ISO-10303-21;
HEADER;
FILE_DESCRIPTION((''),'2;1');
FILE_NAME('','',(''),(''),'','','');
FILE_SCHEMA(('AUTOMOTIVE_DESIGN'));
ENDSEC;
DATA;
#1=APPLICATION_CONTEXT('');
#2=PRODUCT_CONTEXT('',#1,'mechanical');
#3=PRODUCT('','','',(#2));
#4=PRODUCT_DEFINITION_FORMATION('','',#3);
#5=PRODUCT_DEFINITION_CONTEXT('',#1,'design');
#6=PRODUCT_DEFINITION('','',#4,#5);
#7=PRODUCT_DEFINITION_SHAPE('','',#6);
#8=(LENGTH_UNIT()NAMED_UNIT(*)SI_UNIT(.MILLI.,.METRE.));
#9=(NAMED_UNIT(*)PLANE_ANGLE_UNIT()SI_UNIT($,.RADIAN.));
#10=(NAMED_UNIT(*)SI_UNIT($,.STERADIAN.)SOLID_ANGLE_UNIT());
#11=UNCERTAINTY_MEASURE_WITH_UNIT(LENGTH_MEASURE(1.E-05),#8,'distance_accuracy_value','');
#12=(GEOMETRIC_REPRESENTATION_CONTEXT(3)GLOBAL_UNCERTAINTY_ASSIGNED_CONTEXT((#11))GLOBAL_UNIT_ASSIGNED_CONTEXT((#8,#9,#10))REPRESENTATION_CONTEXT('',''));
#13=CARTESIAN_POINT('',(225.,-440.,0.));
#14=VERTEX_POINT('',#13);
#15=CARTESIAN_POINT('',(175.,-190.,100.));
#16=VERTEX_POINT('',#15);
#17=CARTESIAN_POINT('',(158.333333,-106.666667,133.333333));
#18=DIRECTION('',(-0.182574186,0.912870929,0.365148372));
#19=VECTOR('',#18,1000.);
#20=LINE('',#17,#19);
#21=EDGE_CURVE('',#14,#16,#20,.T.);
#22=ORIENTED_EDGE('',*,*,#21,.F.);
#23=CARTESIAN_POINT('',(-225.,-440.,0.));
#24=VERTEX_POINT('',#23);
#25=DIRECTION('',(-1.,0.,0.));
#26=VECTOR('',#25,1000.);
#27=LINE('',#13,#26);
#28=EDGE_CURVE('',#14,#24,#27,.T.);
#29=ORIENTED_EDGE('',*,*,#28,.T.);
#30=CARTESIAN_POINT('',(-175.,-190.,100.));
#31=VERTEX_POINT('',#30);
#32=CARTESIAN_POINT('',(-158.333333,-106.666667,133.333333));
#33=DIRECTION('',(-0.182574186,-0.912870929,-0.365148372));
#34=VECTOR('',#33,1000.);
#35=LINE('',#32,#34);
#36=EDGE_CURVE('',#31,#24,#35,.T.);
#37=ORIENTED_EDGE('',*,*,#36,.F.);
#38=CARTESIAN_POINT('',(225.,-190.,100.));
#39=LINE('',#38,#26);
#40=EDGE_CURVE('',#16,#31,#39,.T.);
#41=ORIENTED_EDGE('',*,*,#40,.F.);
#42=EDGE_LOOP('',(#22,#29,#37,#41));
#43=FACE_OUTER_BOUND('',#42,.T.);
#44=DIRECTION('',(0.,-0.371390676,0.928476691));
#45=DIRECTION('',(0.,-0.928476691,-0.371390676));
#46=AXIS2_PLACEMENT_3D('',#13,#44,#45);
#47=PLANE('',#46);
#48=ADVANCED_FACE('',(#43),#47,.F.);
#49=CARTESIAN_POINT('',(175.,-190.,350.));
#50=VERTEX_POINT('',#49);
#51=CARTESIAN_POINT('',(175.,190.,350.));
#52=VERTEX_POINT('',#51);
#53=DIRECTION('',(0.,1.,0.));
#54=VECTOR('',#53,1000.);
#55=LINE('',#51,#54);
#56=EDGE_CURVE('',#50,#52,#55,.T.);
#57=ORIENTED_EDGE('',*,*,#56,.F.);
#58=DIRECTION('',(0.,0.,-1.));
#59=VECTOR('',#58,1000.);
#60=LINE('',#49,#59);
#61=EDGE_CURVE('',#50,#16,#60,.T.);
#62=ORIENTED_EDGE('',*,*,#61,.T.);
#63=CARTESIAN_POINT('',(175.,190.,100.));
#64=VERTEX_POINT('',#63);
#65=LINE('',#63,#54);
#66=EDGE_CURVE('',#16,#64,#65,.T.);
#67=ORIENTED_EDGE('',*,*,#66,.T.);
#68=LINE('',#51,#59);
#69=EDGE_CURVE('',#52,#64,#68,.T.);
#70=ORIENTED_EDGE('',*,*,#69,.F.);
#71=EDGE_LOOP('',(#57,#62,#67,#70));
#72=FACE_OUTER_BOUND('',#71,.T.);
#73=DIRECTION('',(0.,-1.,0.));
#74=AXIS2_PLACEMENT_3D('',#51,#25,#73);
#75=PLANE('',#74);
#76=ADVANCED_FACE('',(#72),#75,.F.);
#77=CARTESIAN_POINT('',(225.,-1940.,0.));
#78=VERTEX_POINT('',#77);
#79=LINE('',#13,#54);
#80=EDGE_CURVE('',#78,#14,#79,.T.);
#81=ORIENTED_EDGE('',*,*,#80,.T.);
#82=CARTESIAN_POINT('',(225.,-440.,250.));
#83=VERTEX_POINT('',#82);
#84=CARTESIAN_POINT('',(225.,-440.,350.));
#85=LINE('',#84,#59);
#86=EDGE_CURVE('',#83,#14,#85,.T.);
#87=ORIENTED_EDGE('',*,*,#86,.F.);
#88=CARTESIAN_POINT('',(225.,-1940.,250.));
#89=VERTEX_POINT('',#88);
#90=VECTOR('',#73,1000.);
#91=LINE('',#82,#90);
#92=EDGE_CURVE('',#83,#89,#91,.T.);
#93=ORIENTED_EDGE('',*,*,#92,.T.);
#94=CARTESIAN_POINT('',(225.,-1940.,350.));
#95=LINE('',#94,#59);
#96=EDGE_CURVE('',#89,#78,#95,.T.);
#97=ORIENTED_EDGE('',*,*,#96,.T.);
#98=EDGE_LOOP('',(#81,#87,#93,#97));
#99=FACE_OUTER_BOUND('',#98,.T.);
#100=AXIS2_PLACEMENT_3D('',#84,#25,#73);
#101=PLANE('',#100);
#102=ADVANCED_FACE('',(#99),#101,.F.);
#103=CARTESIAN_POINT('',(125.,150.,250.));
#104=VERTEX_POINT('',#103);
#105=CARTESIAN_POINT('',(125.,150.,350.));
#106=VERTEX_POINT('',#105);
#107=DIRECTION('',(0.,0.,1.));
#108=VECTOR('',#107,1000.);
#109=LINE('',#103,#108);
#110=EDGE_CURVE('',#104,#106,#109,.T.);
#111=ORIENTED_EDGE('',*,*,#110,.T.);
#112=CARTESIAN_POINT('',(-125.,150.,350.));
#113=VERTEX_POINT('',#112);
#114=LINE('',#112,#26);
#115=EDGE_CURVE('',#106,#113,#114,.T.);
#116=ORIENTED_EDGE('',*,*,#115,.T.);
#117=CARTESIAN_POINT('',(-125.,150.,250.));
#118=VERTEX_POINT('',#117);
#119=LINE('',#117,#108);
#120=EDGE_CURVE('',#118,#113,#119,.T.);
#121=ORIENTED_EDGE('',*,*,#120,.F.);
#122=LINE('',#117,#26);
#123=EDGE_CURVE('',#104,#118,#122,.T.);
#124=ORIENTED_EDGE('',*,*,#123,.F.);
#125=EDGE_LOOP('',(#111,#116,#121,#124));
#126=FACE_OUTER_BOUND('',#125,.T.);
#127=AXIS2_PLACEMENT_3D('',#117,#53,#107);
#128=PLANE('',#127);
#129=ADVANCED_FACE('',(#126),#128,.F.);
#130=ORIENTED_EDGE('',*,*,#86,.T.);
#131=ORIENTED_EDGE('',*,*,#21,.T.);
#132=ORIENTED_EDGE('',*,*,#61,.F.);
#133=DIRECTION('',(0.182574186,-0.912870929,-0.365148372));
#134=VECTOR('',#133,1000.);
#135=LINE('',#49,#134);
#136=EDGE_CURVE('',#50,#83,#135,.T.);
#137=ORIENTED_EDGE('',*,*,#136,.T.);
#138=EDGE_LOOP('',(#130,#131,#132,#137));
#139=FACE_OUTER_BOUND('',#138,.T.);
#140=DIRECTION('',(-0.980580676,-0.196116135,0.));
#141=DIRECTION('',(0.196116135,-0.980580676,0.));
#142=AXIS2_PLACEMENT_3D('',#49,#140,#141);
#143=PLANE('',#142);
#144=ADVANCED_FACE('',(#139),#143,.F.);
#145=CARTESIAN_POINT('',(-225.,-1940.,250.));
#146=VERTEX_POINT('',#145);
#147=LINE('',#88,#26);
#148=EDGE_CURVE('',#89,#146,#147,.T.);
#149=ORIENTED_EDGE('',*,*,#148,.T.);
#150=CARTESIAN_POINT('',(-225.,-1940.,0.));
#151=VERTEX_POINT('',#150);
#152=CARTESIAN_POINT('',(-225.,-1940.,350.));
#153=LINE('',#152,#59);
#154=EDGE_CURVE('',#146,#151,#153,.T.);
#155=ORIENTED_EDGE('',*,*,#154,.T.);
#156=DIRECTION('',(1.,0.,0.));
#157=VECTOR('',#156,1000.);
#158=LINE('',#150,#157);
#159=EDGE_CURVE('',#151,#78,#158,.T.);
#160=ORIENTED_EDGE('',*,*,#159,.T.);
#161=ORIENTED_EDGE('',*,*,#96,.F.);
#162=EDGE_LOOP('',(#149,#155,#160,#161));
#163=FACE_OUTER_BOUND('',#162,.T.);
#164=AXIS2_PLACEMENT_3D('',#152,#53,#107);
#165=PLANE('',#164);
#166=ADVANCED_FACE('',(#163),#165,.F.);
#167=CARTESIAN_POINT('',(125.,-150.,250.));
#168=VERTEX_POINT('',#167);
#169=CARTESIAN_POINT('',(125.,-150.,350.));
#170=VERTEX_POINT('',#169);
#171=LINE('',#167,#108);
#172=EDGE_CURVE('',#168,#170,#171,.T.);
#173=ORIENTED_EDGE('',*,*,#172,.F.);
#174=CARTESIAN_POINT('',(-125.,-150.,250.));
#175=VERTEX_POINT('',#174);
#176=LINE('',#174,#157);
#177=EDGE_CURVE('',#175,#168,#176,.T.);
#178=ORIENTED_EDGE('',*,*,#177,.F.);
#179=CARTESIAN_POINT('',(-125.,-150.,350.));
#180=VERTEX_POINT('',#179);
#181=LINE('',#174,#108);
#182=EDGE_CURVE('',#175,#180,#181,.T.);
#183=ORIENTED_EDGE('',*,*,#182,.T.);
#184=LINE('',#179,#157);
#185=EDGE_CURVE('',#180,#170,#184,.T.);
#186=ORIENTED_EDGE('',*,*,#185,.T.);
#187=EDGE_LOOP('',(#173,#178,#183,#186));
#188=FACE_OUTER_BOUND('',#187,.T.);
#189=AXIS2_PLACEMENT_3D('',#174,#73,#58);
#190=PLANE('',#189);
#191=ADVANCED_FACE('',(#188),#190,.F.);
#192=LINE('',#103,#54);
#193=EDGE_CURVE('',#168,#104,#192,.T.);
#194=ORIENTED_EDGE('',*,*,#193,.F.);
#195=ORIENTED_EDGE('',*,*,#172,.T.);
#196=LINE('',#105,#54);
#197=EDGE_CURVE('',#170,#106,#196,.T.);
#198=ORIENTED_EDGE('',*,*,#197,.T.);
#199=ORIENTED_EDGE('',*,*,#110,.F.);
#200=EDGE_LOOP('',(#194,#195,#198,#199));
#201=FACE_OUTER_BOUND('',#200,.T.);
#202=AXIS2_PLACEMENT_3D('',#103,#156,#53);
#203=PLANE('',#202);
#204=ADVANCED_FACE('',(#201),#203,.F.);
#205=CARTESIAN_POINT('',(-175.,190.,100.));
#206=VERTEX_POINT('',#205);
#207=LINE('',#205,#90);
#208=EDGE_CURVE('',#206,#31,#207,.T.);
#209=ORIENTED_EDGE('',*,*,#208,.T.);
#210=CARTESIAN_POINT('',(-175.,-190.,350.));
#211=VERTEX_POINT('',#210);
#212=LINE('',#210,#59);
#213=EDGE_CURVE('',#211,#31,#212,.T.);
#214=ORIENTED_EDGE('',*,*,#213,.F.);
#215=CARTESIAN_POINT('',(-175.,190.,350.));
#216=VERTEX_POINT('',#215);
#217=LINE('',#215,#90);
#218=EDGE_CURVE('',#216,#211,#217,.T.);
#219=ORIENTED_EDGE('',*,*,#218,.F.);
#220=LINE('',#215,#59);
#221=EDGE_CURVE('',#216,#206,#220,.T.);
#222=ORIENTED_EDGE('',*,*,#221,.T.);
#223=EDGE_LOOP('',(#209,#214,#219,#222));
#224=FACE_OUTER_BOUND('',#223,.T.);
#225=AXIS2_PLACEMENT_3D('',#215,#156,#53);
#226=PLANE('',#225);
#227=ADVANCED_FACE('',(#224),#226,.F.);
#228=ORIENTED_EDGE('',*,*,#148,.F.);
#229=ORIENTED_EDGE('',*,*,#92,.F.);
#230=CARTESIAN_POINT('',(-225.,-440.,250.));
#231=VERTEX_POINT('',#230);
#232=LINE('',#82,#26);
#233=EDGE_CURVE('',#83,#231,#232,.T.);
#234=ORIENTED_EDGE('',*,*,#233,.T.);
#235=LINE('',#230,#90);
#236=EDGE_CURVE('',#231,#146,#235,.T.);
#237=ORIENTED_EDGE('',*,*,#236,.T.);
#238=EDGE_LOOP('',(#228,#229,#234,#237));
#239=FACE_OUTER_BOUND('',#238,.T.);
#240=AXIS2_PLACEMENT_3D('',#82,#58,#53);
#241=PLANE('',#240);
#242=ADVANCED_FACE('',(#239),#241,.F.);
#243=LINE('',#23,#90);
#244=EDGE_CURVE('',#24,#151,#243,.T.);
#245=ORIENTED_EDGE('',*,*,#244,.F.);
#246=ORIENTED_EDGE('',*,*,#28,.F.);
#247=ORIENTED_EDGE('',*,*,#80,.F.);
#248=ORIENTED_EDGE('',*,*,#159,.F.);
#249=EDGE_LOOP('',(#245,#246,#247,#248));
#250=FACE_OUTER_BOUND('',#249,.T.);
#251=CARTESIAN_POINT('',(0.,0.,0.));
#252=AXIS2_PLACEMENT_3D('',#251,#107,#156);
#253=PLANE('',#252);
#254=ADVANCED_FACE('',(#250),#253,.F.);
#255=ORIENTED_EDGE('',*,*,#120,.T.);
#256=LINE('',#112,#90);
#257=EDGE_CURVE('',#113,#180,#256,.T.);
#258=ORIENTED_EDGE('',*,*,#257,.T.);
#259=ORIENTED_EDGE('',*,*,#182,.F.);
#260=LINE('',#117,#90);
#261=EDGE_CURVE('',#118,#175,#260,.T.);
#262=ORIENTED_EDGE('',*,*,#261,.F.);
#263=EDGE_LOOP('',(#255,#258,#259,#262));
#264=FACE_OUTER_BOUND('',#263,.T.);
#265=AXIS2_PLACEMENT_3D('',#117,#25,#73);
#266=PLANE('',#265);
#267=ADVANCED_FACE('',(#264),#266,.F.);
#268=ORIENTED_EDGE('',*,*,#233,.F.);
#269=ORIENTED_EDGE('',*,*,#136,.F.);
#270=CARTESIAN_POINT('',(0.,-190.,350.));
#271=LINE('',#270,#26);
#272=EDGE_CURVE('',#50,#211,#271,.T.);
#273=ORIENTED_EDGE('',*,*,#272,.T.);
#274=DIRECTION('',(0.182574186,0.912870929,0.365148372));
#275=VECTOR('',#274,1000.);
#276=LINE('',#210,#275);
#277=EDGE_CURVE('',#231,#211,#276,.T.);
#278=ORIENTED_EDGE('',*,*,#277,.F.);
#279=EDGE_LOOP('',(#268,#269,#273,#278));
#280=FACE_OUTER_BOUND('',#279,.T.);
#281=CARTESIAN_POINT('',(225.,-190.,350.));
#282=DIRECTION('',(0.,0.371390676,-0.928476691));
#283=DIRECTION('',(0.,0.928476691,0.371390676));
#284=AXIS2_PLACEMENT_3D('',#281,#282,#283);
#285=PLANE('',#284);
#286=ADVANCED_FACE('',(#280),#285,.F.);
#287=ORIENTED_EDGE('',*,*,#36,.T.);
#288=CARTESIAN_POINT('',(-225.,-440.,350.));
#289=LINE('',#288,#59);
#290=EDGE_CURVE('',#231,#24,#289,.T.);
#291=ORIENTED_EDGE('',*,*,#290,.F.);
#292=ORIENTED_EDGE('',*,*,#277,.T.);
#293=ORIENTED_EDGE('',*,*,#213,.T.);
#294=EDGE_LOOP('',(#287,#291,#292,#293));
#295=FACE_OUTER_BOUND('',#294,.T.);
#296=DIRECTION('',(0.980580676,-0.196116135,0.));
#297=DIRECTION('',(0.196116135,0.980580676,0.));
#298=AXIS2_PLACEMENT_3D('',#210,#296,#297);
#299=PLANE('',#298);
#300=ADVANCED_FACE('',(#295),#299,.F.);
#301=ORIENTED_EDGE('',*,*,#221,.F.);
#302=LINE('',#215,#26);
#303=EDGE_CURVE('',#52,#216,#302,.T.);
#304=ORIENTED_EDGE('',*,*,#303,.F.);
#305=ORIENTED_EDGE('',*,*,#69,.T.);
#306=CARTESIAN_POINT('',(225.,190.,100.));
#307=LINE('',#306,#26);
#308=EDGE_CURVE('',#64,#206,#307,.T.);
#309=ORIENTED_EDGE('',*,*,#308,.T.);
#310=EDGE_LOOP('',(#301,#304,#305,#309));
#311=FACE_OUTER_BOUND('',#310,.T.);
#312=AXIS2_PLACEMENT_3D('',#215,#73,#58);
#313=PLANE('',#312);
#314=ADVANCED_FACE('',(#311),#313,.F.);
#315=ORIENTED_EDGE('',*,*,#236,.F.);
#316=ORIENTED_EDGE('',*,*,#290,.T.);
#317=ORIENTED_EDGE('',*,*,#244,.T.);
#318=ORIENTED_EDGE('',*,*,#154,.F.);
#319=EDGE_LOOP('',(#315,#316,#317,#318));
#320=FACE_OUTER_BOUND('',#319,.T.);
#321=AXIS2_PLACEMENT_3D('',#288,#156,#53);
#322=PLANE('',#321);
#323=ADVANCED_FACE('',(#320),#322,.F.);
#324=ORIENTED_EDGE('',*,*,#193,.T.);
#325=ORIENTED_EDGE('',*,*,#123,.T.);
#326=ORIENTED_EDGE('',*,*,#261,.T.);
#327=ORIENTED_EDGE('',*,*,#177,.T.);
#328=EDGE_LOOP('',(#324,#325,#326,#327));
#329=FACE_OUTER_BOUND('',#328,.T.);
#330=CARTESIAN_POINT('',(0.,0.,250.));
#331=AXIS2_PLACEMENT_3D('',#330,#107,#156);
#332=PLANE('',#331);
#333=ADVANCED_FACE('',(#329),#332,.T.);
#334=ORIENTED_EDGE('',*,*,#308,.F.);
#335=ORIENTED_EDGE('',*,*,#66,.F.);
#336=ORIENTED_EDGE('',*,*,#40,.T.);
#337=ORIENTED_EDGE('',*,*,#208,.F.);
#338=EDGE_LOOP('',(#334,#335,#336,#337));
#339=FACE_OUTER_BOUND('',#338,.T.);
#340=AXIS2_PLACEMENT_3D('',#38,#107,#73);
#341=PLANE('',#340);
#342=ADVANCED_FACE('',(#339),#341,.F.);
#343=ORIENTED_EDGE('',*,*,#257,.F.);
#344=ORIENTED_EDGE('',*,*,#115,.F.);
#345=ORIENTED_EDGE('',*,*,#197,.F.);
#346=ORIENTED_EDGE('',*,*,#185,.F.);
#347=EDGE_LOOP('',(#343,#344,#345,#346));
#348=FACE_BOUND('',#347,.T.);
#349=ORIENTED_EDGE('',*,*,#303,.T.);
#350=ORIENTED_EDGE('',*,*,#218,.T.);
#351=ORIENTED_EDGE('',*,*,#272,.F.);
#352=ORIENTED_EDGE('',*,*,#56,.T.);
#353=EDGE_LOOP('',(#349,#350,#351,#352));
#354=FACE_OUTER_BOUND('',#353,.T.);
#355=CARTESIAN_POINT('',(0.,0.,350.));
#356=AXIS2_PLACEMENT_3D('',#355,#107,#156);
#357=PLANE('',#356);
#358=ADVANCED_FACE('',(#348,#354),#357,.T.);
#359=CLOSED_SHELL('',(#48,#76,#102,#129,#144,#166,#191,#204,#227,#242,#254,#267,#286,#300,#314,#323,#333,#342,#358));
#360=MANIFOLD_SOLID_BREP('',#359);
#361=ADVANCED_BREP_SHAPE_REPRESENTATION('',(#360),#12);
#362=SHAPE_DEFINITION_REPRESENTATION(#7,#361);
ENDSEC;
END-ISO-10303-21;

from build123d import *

# Parameters (mm, degrees)
BOSS_EXTRUDE1_DEPTH = 350
CUT_EXTRUDE1_DEPTH  = 2023.028684267
SKETCH4_W           = 250
SKETCH4_H           = 300
CUT_EXTRUDE2_DEPTH  = 100


with BuildPart() as part:
    # Sketch2 → Boss-Extrude1 (new body)
    with BuildSketch(Plane.XY):
        Polygon((-175, 190), (175, 190), (175, -190), (225, -440), (225, -1940), (-225, -1940), (-225, -440), (-175, -190), align=None)
    extrude(amount=BOSS_EXTRUDE1_DEPTH)

    # Sketch3 → Cut-Extrude1 (cut, through all)
    with BuildSketch(Plane.ZY.offset(225)):
        Polygon((350, -190), (250, -440), (250, -1940), (350, -1940), align=None)
        Polygon((0, -440), (100, -190), (100, 190), (0, 190), align=None)
    extrude(amount=-CUT_EXTRUDE1_DEPTH, mode=Mode.SUBTRACT)

    # Sketch4 → Cut-Extrude2 (cut)
    with BuildSketch(Plane.XY.offset(350)):
        Rectangle(SKETCH4_W, SKETCH4_H)
    extrude(amount=-CUT_EXTRUDE2_DEPTH, mode=Mode.SUBTRACT)


solid = part.part
